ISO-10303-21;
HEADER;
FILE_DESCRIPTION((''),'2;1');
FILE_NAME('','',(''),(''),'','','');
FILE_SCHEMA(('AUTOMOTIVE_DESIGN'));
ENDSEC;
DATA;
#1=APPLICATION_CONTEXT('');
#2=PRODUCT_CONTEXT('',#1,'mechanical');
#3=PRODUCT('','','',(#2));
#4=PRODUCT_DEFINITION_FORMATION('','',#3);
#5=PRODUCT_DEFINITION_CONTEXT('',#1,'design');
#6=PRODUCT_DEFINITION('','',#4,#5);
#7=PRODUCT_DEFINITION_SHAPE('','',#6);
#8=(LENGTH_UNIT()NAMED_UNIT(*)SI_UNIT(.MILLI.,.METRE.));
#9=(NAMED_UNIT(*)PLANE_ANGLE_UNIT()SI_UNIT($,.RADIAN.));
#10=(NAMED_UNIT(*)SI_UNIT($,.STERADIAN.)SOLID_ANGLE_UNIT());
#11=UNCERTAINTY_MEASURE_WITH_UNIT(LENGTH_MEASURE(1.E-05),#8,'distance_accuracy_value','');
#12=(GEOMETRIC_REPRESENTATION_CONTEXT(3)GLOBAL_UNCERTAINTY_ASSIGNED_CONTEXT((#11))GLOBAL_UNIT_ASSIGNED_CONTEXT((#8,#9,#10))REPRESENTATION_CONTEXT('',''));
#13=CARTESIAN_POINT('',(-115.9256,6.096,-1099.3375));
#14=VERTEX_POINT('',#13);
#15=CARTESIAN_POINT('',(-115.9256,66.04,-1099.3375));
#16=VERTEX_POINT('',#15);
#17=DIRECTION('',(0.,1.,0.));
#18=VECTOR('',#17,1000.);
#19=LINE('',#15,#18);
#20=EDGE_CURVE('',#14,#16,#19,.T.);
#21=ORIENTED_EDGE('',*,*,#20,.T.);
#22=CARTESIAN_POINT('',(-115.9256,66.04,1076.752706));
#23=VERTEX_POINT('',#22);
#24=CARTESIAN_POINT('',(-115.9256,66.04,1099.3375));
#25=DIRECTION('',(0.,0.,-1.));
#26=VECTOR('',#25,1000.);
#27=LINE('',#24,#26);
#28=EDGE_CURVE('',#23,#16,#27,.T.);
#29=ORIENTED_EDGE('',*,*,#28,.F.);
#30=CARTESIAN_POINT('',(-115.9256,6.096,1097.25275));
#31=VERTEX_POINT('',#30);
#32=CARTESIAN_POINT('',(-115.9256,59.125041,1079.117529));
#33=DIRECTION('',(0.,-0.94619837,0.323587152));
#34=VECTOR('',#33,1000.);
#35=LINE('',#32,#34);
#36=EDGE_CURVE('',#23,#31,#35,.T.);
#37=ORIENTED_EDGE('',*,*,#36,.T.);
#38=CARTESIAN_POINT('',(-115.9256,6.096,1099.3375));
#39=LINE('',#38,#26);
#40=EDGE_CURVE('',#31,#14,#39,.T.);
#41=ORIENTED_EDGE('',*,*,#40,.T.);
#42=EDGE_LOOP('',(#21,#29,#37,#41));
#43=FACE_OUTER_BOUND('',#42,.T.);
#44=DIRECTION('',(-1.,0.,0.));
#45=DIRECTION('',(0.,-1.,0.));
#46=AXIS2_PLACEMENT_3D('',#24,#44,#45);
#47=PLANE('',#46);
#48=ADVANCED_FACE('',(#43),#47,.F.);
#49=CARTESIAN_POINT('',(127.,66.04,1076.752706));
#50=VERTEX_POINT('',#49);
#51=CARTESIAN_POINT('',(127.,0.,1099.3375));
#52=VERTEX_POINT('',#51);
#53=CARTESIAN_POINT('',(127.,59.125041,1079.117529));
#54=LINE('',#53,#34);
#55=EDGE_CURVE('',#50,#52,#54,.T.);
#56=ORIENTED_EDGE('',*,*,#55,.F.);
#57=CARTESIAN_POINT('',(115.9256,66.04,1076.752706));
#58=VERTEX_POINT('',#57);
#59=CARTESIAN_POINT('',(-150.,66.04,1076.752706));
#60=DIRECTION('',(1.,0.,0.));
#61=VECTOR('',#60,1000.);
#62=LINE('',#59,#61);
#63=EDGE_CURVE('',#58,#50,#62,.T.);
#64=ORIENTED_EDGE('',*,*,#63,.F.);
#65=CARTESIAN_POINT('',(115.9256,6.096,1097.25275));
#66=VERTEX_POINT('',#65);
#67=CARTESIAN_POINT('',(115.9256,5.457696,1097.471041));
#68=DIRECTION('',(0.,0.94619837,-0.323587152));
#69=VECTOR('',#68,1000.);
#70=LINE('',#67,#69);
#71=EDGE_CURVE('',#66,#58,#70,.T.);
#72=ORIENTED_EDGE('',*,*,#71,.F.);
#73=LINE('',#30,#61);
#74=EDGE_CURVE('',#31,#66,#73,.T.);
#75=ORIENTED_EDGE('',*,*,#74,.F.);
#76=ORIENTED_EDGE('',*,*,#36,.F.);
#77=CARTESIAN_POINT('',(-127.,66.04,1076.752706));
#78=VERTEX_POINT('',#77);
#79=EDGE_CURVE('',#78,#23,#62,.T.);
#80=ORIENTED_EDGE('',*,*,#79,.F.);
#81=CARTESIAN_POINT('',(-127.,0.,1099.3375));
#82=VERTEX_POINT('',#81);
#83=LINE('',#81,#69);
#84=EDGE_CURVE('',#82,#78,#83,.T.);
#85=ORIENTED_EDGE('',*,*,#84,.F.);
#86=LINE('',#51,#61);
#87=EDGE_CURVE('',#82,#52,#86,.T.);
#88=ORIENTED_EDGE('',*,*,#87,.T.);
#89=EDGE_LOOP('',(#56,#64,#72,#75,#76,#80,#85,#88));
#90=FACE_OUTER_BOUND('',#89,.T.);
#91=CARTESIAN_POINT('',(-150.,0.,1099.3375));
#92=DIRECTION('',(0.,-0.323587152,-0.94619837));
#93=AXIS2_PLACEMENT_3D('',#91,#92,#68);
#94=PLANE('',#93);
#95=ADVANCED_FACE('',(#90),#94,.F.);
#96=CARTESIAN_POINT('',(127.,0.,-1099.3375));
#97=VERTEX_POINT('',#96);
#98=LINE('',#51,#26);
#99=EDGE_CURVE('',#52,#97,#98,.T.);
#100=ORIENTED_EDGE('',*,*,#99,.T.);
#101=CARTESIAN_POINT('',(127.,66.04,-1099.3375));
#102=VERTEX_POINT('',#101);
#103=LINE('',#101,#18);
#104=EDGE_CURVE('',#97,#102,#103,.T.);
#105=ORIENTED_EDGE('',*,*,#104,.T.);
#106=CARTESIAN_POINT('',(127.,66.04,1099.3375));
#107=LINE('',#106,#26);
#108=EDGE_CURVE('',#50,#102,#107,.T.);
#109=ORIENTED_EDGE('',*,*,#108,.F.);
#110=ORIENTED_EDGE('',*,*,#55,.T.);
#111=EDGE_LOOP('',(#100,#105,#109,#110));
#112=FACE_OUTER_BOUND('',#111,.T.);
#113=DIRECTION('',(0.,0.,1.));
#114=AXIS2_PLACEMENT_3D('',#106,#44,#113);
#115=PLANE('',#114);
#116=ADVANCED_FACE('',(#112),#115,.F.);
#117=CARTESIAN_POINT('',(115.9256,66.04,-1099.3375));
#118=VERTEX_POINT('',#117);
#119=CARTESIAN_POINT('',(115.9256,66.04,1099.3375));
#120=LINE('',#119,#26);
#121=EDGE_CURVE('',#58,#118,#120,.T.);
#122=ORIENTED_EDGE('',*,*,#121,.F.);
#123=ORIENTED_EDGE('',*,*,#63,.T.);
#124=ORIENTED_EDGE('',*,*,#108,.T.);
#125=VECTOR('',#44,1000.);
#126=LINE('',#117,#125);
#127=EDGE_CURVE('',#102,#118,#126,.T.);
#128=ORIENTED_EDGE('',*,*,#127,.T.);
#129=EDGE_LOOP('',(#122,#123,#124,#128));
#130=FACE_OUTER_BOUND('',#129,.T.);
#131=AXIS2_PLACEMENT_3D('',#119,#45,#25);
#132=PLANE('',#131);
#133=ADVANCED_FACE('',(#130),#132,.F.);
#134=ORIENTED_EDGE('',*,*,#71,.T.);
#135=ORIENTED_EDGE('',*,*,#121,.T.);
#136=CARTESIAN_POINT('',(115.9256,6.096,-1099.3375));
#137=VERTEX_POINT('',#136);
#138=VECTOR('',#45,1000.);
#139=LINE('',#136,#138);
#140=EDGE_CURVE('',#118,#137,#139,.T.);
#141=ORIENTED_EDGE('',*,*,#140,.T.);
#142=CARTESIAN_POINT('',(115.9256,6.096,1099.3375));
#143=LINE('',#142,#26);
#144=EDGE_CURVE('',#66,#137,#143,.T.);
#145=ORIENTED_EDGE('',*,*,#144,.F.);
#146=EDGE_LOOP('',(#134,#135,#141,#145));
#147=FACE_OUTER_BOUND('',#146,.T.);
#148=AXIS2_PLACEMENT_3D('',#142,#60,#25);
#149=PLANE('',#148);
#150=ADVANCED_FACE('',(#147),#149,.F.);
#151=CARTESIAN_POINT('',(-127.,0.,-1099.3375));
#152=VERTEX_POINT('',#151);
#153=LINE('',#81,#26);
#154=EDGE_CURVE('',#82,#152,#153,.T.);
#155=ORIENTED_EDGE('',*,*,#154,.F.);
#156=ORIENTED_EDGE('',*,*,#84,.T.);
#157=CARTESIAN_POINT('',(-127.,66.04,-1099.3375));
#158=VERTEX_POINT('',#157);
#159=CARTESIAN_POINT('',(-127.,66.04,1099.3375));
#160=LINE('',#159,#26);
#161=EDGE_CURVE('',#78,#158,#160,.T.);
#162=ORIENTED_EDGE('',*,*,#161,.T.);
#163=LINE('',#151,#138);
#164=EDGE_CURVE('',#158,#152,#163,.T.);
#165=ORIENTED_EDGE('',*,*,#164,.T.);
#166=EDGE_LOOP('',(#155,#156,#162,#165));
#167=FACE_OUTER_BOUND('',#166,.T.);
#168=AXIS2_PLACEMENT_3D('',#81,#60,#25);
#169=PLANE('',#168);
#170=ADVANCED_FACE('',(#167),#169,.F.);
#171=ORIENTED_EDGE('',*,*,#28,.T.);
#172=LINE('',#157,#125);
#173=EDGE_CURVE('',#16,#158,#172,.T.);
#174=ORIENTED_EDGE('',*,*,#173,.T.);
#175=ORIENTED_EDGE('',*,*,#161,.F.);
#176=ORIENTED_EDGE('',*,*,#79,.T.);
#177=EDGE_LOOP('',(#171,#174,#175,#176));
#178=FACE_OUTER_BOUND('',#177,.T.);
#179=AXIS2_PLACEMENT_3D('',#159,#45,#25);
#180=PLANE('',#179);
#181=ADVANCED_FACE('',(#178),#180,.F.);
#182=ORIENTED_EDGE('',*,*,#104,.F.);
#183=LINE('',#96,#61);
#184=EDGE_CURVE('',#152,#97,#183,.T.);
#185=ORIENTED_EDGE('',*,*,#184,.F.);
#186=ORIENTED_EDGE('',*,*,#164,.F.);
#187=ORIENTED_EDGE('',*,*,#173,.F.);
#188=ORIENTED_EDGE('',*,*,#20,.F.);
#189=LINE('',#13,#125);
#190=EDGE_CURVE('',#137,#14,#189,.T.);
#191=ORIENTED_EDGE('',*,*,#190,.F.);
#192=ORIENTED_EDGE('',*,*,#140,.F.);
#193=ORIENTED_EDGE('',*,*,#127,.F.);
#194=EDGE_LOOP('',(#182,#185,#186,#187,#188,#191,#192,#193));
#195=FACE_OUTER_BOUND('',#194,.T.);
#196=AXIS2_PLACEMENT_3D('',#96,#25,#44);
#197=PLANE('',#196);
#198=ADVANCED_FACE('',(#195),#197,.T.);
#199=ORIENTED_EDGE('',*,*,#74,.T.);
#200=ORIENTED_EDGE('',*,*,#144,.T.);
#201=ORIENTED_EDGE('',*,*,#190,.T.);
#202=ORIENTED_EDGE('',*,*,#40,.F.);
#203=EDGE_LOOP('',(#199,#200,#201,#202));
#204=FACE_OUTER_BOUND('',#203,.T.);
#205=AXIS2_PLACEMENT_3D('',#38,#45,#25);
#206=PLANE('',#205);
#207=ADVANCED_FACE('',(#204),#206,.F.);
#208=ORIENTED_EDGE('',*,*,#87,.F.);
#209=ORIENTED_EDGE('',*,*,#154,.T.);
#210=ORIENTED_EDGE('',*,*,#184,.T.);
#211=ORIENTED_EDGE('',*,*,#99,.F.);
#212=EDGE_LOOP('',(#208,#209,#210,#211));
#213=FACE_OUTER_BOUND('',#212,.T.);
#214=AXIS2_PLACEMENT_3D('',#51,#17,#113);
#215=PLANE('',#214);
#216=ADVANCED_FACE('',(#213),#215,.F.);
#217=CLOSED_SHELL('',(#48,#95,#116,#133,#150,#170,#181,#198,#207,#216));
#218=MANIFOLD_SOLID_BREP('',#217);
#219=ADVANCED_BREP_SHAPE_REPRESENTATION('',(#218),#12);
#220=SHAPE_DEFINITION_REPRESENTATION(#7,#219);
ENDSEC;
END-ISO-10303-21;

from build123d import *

# Parameters (mm, degrees)
BOSS_EXTRUDE1_DEPTH = 1099.3375
CUT_EXTRUDE1_DEPTH  = 150


with BuildPart() as part:
    # Sketch1 → Boss-Extrude1 (new, symmetric)
    with BuildSketch(Plane.XY):
        Polygon((127, 0), (-127, 0), (-127, 66.04), (-115.9256, 66.04), (-115.9256, 6.096), (115.9256, 6.096), (115.9256, 66.04), (127, 66.04), align=None)
    extrude(amount=BOSS_EXTRUDE1_DEPTH, both=True)

    # Sketch2 → Cut-Extrude1 (cut, symmetric)
    with BuildSketch(Plane(origin=(0, 0, 0), x_dir=(0, 0, -1), z_dir=(1, 0, 0))):
        Polygon((-1099.3375, 0), (-1076.752705704, 66.04), (-1099.3375, 66.04), align=None)
    extrude(amount=CUT_EXTRUDE1_DEPTH, both=True, mode=Mode.SUBTRACT)


solid = part.part
